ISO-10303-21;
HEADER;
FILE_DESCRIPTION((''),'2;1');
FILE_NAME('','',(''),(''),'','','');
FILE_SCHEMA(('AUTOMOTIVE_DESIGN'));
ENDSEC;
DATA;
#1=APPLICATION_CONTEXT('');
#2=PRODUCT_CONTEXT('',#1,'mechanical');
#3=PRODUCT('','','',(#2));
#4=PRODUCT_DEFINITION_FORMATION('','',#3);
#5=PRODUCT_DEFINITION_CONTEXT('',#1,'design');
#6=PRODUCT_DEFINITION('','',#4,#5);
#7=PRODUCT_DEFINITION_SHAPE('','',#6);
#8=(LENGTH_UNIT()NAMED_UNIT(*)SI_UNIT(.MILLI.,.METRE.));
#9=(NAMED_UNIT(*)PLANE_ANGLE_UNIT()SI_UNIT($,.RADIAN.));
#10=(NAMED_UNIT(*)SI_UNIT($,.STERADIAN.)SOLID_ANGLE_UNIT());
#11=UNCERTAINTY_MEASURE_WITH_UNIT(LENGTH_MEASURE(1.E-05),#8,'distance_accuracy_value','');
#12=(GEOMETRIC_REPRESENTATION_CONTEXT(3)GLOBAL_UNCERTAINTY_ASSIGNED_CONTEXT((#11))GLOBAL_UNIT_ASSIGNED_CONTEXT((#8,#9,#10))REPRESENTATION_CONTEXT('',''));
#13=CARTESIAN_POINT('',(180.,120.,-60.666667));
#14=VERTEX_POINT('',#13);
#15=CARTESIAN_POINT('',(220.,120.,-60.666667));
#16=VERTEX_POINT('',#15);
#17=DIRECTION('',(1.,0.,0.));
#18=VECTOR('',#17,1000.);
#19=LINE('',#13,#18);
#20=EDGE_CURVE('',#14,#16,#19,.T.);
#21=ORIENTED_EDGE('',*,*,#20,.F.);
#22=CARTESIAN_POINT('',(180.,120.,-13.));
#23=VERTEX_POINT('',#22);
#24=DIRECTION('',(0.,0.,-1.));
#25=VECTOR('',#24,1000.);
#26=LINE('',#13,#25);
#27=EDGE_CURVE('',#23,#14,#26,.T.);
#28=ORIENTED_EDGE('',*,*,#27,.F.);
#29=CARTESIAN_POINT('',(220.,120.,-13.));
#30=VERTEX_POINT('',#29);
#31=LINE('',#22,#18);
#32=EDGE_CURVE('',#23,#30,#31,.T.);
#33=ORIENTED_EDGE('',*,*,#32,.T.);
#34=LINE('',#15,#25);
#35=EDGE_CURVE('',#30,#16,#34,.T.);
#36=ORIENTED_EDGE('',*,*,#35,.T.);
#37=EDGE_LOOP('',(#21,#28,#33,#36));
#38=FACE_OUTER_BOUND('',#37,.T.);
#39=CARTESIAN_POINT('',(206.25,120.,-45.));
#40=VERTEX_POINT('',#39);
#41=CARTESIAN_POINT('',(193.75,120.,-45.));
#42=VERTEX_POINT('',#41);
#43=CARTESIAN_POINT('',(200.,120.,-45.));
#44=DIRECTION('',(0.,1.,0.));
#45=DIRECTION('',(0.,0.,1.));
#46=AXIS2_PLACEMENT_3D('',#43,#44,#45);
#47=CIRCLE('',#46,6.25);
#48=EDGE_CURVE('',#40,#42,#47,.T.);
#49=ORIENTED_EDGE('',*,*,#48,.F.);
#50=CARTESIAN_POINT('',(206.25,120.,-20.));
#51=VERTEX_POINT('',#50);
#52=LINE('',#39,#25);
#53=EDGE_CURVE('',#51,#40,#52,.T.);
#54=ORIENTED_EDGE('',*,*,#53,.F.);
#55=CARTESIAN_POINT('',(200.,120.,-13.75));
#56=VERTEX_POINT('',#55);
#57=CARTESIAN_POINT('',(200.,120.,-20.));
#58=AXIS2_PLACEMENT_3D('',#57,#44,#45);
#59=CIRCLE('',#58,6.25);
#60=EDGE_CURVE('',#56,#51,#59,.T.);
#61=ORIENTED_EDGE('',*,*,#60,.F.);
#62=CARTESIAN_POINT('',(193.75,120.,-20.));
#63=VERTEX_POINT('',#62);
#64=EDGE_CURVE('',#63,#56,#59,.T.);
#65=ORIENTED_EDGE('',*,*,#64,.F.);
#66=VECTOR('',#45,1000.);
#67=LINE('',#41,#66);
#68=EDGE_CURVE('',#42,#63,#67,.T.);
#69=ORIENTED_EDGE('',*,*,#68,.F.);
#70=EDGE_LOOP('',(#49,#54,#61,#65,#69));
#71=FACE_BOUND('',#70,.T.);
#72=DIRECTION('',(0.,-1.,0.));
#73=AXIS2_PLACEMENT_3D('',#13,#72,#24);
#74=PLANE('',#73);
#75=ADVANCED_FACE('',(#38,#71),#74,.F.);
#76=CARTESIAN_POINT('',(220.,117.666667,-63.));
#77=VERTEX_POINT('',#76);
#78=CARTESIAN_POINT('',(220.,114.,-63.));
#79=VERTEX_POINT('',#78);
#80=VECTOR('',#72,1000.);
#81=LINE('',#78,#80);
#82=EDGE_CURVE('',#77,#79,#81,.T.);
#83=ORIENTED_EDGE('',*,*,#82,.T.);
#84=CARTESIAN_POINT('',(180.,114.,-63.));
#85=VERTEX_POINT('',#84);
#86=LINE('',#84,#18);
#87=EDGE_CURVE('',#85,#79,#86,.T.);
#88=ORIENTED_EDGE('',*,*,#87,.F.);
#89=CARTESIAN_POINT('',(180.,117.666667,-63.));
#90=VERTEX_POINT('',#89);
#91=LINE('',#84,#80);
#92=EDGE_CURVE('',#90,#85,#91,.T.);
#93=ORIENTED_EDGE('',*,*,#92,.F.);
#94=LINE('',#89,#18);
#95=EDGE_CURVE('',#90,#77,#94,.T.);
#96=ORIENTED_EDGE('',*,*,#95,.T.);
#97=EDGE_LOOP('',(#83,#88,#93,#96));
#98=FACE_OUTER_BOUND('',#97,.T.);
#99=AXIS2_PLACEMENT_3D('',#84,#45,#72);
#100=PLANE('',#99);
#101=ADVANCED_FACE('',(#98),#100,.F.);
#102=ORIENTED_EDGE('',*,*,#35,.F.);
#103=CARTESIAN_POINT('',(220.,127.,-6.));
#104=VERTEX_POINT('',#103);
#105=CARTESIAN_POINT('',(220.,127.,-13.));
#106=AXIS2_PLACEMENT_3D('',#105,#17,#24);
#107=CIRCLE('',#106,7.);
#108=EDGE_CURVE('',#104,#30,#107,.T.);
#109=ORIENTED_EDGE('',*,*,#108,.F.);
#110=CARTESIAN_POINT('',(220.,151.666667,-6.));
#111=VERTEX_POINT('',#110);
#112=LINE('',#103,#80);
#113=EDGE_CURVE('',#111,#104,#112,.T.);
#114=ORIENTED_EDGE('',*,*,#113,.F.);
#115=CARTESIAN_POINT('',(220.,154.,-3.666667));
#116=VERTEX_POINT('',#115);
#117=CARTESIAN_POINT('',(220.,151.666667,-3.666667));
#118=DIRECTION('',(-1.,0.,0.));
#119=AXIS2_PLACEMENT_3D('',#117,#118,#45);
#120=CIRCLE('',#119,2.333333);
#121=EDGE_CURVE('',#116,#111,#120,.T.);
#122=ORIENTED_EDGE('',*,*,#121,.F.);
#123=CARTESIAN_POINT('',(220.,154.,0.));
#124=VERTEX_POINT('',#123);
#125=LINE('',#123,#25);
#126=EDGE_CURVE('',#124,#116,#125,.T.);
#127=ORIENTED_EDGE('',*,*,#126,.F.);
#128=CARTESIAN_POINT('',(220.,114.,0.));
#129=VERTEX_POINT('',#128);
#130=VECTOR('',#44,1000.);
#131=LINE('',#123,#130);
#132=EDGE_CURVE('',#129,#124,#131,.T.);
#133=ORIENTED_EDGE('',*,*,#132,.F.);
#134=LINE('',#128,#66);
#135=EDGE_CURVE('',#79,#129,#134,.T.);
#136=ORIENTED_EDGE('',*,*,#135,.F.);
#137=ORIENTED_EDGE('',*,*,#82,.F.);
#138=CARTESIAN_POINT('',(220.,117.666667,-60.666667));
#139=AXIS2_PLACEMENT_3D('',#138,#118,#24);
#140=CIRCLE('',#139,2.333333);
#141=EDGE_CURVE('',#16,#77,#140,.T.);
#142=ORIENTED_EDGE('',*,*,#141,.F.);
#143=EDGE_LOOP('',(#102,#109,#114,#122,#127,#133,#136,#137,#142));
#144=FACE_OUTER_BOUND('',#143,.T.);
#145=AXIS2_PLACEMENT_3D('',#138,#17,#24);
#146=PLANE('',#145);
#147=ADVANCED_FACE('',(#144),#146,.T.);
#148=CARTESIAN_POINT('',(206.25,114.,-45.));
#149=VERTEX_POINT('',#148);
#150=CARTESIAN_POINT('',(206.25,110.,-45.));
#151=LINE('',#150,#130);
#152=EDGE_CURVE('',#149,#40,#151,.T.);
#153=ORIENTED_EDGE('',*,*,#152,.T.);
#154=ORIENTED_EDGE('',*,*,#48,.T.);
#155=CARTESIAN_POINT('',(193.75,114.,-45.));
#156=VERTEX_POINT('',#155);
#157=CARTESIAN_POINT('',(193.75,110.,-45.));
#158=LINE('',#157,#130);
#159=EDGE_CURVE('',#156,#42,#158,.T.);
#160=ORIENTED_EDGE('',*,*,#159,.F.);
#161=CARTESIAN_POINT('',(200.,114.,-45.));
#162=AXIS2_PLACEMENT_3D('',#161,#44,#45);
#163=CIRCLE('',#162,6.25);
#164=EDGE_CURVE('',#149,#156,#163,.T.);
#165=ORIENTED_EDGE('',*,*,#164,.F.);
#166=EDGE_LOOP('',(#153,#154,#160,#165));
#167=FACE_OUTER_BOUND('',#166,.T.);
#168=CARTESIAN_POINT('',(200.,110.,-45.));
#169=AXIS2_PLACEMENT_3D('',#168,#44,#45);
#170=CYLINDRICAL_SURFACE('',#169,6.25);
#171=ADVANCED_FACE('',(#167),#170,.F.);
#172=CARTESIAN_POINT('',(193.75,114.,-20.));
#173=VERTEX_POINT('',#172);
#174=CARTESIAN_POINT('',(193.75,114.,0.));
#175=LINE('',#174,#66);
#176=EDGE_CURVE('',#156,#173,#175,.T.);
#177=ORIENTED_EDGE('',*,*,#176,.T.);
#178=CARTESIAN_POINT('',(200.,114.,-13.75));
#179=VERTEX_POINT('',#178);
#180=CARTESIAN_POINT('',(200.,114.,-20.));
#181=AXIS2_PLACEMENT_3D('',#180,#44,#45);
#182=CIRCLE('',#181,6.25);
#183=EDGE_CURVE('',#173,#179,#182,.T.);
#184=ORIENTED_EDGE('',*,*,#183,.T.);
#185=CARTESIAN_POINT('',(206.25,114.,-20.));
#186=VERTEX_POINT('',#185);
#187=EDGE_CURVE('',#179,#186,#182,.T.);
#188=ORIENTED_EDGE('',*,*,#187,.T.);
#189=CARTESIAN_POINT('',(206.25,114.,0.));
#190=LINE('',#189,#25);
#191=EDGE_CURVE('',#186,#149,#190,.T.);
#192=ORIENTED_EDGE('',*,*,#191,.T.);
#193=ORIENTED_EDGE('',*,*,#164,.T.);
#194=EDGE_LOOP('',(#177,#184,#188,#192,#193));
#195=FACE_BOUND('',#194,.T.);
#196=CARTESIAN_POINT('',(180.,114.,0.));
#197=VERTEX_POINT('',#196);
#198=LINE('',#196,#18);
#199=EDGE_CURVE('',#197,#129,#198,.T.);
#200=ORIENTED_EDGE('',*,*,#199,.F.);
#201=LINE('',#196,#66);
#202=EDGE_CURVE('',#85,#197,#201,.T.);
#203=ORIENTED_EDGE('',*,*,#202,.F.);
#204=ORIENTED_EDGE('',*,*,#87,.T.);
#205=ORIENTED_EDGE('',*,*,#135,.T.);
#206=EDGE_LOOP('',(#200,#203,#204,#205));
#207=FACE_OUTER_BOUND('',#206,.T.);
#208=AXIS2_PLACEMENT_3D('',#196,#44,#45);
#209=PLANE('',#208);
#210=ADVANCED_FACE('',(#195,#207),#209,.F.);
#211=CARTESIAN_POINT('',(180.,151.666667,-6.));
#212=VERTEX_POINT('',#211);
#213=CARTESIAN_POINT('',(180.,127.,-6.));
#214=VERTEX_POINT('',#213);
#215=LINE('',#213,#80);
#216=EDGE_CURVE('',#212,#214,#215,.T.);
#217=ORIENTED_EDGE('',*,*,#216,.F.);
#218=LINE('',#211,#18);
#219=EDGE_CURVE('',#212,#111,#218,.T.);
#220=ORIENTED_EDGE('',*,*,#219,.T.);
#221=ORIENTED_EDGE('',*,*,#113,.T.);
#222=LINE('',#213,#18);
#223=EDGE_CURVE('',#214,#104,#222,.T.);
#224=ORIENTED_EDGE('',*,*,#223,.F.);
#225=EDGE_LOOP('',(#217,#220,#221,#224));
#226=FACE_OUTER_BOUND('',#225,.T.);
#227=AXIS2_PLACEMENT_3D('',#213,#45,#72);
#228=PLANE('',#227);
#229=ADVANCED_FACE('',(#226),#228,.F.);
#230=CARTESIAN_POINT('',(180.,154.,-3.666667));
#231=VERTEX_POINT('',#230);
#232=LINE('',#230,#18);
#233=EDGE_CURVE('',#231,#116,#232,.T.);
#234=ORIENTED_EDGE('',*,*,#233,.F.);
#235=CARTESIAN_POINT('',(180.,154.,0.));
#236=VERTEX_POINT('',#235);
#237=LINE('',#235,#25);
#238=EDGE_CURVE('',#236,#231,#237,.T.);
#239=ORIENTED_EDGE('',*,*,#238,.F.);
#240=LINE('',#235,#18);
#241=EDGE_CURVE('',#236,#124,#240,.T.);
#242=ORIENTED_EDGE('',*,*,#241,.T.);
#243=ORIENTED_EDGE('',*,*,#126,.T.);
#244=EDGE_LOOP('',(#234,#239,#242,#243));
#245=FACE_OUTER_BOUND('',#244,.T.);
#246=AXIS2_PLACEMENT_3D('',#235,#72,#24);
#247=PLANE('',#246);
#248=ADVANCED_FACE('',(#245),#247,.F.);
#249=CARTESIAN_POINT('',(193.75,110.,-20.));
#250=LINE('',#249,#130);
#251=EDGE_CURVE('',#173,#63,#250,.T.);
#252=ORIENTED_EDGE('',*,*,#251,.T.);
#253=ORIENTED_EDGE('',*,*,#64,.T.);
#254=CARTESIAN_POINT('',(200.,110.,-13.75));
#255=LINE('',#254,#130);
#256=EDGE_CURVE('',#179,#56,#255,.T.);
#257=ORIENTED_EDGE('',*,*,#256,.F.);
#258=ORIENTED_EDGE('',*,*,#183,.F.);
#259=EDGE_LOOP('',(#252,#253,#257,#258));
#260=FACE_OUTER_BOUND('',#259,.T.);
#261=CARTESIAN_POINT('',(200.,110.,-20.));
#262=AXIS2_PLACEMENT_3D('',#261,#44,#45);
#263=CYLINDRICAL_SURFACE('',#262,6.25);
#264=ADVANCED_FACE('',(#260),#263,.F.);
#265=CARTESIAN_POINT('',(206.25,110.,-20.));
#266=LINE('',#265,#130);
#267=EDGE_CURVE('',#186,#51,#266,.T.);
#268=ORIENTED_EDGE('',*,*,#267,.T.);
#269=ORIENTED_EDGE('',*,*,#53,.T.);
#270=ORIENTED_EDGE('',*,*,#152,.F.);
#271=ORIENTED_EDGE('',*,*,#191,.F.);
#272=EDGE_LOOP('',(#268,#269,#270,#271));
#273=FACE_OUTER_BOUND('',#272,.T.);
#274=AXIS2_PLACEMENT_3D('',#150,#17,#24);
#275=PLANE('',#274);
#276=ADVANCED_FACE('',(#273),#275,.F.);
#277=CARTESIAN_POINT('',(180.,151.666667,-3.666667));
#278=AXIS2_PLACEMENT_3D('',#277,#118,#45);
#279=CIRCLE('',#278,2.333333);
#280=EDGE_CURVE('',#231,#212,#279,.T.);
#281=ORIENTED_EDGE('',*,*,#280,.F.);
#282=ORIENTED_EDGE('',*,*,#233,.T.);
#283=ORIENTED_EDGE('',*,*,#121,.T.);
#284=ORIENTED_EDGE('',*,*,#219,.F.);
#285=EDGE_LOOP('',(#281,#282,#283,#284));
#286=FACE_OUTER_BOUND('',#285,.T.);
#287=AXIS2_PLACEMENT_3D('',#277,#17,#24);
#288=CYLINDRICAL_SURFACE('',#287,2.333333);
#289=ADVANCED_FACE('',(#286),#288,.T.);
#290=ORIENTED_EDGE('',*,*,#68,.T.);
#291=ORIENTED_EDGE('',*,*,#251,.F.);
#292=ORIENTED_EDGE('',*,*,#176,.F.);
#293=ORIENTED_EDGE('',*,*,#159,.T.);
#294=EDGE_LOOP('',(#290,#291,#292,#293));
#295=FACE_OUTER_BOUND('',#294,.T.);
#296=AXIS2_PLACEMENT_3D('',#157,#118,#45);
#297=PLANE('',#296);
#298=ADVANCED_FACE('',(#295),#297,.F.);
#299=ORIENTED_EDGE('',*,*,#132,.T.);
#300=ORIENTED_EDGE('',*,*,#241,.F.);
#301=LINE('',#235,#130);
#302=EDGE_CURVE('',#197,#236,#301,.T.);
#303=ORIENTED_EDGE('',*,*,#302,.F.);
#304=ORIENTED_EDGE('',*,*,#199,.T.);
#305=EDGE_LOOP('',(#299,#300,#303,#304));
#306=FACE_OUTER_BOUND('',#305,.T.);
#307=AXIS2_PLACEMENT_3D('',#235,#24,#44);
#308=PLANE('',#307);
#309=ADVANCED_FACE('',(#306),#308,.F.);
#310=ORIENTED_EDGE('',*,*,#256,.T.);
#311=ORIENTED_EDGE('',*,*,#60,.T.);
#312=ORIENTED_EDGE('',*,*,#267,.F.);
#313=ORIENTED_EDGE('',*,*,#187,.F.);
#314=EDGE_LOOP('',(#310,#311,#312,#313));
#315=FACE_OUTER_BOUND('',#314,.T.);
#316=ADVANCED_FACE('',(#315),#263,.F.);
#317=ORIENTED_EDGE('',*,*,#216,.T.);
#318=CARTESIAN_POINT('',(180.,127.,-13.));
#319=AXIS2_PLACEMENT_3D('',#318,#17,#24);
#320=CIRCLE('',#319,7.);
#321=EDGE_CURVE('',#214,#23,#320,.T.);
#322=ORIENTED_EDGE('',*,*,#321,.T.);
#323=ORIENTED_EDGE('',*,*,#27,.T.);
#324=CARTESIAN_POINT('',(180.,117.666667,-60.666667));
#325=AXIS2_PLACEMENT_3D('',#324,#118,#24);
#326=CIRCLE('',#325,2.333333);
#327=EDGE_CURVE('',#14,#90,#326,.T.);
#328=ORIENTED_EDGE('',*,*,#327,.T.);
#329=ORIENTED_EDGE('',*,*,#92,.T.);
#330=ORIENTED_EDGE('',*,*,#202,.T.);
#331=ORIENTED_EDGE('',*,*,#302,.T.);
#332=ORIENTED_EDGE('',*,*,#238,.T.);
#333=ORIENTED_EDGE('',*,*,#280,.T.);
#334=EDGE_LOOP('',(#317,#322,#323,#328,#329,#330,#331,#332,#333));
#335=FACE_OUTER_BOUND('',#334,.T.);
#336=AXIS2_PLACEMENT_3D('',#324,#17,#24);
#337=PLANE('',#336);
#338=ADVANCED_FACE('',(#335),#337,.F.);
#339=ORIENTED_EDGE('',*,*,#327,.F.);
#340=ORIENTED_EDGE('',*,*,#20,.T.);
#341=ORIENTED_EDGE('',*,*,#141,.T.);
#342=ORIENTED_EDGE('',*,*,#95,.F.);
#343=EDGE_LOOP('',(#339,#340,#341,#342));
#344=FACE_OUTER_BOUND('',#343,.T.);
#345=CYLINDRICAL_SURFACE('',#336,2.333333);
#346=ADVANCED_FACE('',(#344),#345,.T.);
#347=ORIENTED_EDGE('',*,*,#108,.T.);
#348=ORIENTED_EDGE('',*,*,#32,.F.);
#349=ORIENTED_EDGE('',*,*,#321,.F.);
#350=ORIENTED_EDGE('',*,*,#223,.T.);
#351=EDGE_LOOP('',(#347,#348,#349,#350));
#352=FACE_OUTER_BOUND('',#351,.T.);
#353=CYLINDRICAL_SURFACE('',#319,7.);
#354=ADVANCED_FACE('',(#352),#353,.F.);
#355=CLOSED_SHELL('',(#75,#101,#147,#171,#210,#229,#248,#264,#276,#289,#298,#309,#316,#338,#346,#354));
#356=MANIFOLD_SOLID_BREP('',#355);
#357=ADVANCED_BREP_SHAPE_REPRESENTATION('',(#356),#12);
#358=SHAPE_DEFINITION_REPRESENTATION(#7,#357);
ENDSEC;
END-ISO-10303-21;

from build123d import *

# Parameters (mm, degrees)
GB_T706_2008_63_X_40_X_6_1_DEPTH = 40
CUT_EXTRUDE_1_DEPTH              = 10


with BuildPart() as part:
    # Sketch1 → 热轧不等边角钢gb∕t706-2008 63 X 40 X 6(1) (new body)
    with BuildSketch(Plane(origin=(220, 114, 0), x_dir=(0, 1, 0), z_dir=(-1, 0, 0))):
        with BuildLine():
            Line((0, 0), (0, 63))
            Line((0, 63), (3.666666667, 63))
            ThreePointArc((3.666666667, 63), (5.316582489, 62.316582489), (6, 60.666666667))
            Line((6, 60.666666667), (6, 13))
            ThreePointArc((6, 13), (8.050252532, 8.050252532), (13, 6))
            Line((13, 6), (37.666666667, 6))
            ThreePointArc((37.666666667, 6), (39.316582489, 5.316582489), (40, 3.666666667))
            Line((40, 3.666666667), (40, 0))
            Line((40, 0), (0, 0))
        make_face()
    extrude(amount=GB_T706_2008_63_X_40_X_6_1_DEPTH)

    # 草图2 → 切除-拉伸1 (cut)
    with BuildSketch(Plane(origin=(0, 120, 0), x_dir=(1, 0, 0), z_dir=(0, 1, 0))):
        with BuildLine():
            Line((206.25, 45), (206.25, 20))
            ThreePointArc((206.25, 20), (200, 13.75), (193.75, 20))
            Line((193.75, 20), (193.75, 45))
            ThreePointArc((193.75, 45), (200, 51.25), (206.25, 45))
        make_face()
    extrude(amount=-CUT_EXTRUDE_1_DEPTH, mode=Mode.SUBTRACT)


solid = part.part
